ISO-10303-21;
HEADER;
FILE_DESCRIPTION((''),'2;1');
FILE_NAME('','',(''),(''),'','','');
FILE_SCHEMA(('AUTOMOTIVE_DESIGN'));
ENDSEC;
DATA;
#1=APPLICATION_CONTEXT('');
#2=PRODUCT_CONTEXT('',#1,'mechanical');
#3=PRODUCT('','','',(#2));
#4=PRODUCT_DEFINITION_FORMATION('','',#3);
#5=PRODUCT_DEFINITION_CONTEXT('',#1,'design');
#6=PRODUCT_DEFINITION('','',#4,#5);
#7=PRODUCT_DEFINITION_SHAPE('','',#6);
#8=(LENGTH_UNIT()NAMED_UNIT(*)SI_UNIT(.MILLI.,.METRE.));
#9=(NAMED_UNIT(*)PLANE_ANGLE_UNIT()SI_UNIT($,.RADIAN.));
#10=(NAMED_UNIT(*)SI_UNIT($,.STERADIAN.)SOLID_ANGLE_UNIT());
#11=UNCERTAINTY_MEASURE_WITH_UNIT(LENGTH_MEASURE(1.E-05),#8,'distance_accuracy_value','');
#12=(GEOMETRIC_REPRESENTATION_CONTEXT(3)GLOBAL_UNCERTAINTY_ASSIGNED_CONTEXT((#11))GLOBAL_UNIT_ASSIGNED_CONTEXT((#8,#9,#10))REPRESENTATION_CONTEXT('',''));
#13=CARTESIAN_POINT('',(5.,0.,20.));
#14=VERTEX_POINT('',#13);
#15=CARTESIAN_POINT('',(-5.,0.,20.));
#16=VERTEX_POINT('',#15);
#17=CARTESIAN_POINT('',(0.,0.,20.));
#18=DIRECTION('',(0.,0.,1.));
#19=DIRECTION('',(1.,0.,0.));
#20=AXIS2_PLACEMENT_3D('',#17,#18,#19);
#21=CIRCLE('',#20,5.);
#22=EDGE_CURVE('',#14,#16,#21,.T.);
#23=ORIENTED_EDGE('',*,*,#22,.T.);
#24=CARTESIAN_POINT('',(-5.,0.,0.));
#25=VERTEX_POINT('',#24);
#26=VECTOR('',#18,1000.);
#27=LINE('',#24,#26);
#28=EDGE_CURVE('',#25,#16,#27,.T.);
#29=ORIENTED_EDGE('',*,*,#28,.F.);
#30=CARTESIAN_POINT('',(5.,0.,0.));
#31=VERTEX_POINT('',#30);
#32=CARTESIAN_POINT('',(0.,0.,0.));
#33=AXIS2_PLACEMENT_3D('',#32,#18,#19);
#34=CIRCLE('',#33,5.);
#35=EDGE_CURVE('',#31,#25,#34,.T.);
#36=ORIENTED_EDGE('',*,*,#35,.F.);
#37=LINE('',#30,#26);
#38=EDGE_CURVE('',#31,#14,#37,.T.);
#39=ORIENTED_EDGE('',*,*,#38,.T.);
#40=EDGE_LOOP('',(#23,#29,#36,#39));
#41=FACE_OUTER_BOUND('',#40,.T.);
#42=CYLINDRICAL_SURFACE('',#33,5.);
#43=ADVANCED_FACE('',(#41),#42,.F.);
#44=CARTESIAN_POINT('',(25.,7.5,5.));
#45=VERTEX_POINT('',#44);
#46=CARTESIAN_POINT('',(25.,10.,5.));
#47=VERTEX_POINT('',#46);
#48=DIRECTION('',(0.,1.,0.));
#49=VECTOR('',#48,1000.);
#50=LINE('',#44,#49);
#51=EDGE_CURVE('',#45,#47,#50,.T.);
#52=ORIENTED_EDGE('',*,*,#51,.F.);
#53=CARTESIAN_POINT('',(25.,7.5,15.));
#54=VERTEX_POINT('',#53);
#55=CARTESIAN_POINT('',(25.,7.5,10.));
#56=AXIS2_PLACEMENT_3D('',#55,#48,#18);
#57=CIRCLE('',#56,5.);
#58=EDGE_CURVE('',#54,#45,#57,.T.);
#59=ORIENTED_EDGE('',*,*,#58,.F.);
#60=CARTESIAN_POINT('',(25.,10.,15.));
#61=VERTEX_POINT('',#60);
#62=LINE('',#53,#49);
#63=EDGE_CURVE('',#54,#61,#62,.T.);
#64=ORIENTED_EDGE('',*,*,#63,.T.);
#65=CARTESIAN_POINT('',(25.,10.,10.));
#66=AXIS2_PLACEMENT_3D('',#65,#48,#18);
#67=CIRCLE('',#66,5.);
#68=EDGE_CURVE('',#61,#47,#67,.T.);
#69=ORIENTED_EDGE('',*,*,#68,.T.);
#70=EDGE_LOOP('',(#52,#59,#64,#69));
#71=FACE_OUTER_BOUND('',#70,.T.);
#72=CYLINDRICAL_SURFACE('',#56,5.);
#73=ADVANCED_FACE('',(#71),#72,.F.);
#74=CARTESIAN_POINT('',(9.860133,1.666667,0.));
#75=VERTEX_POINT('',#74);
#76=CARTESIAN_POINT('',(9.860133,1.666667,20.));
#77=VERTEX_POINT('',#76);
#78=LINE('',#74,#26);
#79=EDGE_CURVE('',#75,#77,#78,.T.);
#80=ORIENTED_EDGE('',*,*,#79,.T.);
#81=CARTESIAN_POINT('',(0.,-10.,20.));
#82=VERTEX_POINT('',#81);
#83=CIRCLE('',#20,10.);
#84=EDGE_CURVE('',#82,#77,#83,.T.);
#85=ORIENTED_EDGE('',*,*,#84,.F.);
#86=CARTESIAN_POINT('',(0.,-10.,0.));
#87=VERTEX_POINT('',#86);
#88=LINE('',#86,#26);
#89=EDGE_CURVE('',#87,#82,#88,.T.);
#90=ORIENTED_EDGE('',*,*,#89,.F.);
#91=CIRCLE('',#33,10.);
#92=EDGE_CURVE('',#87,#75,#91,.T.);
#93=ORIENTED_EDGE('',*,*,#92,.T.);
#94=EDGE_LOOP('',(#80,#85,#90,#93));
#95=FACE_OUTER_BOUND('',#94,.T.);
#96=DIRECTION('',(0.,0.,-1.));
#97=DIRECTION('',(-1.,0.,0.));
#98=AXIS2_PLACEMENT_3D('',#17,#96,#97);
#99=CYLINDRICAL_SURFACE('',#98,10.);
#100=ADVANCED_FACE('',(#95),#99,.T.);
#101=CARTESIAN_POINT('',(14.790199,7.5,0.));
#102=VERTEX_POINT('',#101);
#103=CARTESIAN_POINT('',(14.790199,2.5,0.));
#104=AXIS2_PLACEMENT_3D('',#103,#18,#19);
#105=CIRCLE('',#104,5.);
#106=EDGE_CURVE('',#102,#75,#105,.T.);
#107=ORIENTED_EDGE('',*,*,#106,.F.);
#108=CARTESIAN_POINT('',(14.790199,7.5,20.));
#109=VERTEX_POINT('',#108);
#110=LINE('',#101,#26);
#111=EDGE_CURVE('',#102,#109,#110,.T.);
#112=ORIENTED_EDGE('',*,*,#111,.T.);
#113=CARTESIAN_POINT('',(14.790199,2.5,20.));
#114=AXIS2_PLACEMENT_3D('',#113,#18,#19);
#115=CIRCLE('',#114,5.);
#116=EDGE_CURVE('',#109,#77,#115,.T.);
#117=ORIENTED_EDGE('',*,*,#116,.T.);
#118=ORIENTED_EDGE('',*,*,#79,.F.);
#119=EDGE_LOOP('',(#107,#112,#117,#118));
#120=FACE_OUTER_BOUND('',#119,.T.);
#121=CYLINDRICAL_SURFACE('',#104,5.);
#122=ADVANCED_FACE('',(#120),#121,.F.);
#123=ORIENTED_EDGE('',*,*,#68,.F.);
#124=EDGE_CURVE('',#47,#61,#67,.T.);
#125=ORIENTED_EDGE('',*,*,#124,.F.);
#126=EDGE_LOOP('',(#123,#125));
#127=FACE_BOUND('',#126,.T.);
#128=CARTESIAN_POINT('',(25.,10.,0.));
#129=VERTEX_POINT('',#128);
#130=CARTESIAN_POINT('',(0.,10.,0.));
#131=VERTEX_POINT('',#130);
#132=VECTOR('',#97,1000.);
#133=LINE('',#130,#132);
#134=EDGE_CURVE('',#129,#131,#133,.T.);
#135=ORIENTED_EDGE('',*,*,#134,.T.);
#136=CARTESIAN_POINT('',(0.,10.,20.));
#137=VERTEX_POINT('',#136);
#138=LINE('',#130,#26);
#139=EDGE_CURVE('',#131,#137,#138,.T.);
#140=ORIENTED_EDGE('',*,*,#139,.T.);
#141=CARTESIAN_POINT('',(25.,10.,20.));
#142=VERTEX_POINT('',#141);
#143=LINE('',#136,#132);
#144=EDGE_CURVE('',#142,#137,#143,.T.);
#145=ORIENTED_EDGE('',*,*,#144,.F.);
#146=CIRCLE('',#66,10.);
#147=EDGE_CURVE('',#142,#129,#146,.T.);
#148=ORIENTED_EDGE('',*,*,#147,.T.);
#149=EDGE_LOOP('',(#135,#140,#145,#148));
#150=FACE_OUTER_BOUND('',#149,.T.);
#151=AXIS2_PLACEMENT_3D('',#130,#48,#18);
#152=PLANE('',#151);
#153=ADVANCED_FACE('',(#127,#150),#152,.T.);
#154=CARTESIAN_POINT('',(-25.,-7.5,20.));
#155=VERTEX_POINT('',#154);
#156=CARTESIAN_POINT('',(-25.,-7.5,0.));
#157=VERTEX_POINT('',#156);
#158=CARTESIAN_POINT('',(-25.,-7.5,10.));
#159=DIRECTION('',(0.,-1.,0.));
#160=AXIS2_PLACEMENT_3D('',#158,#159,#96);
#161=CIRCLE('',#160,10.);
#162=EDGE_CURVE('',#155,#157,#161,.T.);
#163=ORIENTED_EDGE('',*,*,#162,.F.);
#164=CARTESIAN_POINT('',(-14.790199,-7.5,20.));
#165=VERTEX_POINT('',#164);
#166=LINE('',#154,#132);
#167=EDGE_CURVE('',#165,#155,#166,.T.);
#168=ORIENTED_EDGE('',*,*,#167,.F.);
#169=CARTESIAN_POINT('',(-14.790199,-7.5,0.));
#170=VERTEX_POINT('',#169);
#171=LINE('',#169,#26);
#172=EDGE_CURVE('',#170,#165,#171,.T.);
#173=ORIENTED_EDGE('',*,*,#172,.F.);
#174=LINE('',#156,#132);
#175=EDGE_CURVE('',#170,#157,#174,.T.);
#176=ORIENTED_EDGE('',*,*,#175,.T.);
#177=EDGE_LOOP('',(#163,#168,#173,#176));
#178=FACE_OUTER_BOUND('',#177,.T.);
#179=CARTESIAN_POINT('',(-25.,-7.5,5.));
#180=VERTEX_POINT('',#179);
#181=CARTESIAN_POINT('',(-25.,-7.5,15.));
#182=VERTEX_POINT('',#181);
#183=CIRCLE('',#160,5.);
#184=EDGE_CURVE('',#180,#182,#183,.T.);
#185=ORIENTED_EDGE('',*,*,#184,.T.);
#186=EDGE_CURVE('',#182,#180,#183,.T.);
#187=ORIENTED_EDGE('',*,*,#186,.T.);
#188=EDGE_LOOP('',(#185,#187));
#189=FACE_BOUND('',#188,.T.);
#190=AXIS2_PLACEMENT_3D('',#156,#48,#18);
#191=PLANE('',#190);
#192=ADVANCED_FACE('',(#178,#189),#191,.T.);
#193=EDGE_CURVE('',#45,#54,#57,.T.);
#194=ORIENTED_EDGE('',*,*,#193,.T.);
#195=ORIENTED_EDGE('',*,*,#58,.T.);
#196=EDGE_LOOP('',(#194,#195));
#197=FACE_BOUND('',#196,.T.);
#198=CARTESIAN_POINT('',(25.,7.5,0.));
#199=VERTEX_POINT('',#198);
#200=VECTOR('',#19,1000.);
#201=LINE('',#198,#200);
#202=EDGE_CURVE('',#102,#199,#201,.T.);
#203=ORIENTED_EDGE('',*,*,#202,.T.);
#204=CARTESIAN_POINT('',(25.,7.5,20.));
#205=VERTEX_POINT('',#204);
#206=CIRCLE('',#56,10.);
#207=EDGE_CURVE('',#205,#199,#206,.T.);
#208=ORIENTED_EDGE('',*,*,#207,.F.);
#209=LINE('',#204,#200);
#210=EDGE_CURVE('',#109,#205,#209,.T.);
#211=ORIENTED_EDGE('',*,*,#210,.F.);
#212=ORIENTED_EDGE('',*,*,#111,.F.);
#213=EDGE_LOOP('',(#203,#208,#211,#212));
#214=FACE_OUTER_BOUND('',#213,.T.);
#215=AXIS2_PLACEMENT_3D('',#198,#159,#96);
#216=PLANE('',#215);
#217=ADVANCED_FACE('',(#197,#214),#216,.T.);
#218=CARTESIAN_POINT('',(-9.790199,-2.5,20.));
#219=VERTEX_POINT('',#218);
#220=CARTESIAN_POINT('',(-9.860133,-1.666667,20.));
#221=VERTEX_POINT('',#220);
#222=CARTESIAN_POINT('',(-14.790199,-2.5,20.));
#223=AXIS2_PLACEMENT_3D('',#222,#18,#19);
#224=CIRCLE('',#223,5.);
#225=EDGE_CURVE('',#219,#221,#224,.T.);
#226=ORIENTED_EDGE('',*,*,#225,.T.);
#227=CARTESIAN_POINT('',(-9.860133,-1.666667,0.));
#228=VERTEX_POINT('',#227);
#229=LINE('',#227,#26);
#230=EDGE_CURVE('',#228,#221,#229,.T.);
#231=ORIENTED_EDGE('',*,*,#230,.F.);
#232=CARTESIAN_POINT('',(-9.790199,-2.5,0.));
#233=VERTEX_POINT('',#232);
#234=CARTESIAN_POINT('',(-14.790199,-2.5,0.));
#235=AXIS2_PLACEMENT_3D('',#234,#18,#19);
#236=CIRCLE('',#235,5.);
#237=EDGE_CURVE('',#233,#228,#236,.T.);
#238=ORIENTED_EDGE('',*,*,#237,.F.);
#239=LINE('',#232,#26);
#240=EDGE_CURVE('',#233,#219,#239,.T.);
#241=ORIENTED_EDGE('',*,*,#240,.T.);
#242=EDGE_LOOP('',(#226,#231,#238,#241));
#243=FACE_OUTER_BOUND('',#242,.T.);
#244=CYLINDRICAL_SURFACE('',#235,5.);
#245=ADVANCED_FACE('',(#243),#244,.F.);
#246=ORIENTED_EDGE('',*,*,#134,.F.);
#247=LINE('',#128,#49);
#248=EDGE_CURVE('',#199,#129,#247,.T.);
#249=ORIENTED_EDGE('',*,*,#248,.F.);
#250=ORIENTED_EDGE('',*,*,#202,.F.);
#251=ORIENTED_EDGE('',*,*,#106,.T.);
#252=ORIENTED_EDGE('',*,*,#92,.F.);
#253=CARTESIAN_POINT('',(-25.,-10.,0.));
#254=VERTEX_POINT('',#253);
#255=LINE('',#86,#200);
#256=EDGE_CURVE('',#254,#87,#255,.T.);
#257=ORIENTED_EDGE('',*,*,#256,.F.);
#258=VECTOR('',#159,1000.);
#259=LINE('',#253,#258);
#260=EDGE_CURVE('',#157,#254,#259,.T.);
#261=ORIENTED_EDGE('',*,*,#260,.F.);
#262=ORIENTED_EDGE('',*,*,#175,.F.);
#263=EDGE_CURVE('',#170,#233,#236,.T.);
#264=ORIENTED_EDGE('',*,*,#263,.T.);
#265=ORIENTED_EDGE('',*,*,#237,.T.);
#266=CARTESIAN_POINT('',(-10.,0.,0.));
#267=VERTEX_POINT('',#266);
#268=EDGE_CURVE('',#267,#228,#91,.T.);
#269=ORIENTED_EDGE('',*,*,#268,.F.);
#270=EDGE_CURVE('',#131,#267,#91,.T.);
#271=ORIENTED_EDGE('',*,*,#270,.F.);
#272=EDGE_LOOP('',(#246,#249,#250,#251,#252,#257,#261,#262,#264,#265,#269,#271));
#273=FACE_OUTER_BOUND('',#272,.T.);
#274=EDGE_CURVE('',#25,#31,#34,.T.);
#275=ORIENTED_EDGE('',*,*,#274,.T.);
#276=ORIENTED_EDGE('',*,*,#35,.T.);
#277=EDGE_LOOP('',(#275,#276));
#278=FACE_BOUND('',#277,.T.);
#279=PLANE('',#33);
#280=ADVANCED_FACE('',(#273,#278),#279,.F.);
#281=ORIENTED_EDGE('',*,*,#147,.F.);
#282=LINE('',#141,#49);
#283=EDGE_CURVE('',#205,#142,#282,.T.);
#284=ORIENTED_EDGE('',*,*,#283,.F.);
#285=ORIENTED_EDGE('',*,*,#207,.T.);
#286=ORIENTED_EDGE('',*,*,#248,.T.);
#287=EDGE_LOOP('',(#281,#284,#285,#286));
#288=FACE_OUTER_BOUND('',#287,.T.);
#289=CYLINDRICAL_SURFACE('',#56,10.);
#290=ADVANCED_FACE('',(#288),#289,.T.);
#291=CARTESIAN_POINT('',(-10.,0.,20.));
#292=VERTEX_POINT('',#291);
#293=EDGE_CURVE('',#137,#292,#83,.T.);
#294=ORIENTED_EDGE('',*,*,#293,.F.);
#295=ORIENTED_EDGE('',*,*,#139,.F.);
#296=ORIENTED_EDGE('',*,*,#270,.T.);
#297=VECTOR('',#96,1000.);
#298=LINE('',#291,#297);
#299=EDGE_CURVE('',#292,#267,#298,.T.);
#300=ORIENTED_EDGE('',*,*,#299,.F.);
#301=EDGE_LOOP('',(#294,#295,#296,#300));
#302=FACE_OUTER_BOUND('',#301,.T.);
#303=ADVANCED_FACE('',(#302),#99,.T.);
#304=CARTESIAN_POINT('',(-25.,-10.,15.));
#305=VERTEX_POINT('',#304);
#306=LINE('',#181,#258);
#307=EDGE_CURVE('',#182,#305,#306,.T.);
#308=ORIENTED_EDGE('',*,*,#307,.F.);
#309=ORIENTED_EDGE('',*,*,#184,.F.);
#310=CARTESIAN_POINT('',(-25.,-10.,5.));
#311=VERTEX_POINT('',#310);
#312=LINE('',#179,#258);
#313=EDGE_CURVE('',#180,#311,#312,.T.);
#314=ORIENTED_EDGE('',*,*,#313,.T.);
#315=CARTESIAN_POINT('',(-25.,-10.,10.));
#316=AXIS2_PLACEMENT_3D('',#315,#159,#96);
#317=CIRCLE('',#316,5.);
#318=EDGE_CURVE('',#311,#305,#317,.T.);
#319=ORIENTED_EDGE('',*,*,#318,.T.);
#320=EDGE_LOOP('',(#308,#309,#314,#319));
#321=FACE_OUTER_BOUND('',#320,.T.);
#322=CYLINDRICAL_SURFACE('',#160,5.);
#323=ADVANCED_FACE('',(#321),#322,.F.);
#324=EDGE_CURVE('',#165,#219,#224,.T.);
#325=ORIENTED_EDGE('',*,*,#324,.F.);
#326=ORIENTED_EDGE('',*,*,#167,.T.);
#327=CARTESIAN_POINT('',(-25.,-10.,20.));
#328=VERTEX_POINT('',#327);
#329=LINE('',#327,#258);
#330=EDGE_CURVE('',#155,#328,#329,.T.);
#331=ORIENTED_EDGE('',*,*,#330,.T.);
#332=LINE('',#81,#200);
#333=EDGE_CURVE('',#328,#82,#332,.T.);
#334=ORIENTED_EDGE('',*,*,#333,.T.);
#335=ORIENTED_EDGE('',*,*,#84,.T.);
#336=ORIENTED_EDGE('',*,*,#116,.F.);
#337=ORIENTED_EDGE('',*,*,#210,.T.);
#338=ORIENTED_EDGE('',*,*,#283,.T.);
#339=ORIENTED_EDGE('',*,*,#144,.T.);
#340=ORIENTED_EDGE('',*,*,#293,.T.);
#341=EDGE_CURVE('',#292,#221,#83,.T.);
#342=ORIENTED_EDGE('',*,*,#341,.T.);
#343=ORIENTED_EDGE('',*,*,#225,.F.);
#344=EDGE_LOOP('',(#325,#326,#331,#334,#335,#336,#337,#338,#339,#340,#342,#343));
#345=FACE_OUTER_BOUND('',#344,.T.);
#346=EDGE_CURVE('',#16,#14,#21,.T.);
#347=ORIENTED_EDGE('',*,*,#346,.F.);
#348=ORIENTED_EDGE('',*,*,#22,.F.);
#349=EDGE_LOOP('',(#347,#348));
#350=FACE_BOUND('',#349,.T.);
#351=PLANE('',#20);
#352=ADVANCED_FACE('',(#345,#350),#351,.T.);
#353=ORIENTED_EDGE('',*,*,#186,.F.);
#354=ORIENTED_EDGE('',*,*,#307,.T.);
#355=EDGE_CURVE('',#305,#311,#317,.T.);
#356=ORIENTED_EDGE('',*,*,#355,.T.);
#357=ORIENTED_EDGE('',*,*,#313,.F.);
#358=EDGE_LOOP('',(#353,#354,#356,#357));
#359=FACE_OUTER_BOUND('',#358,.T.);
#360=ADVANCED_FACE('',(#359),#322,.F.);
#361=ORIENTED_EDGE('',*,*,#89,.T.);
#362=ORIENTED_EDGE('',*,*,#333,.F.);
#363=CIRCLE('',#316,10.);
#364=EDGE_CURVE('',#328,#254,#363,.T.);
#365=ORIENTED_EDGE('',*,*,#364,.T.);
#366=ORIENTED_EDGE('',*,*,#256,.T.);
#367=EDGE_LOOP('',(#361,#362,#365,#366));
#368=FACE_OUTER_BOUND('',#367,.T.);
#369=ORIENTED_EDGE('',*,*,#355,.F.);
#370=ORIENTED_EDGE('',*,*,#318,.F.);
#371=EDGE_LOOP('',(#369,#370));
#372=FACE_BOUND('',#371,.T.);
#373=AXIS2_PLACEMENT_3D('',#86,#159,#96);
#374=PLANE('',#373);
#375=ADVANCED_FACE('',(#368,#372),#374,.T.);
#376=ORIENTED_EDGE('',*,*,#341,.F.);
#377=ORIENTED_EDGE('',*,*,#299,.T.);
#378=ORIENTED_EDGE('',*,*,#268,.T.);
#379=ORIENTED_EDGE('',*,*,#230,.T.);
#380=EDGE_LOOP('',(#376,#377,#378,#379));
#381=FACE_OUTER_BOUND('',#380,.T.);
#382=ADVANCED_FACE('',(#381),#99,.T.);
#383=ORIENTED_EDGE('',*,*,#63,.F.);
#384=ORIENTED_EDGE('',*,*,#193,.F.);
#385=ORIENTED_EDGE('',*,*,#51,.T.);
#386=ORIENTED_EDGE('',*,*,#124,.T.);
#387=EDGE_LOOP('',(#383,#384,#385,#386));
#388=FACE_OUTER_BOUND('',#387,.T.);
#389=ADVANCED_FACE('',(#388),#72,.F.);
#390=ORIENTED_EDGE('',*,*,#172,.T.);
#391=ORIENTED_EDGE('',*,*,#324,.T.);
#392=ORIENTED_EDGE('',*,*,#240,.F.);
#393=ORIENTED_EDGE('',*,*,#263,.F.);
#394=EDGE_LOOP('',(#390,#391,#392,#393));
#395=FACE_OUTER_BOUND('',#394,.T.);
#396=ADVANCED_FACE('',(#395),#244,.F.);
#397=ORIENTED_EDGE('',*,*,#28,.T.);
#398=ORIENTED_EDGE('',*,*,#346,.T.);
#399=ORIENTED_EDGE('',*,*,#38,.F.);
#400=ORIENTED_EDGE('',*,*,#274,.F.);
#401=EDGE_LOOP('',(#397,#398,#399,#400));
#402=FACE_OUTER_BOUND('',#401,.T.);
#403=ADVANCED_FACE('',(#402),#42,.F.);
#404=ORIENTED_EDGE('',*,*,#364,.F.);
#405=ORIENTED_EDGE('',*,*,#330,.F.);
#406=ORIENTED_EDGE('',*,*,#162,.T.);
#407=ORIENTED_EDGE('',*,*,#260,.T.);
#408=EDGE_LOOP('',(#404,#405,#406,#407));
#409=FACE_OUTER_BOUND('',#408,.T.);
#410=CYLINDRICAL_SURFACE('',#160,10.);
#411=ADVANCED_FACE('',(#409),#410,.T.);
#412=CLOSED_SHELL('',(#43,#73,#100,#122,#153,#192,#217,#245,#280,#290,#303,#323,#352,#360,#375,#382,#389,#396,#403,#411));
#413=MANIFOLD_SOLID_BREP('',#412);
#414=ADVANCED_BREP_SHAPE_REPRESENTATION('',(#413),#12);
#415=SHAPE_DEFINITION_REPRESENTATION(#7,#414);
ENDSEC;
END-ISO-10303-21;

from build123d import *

# Parameters (mm, degrees)
HUB_SKETCH_20_R            = 10
HUB_CYLINDER_20_DEPTH      = 20
FIRST_START                = -20
FIRST_ARM_DEPTH            = 20
SECOND_START               = -20
SECOND_ARM_DEPTH           = 20
TAB_A_DEPTH                = 2.5
TAB_B_DEPTH                = 2.5
TAB_B_HOLE_SKETCH_10_R     = 5
TAB_B_HOLE_10_DEPTH        = 2.5
TAB_A_HOLE_SKETCH_10_R     = 5
TAB_A_HOLE_10_DEPTH        = 2.5
HUB_CROSS_BORE_SKETCH_10_R = 5
HUB_CROSS_BORE_10_DEPTH    = 20


with BuildPart() as part:
    # Hub Sketch Ø20 → Hub Cylinder Ø20 (new body)
    with BuildSketch(Plane.XY):
        Circle(HUB_SKETCH_20_R)
    extrude(amount=HUB_CYLINDER_20_DEPTH)

    # First Arm Sketch → First Arm (add)
    with BuildSketch(Plane.XY.offset(20).offset(FIRST_START)):
        with BuildLine():
            Line((0, 10), (25, 10))
            Line((25, 10), (25, 7.5))
            Line((25, 7.5), (6.614378278, 7.5))
            ThreePointArc((6.614378278, 7.5), (3.535533906, 9.354143467), (0, 10))
        make_face()
        with BuildLine():
            Line((0, -10), (-25, -10))
            Line((-25, -10), (-25, -7.5))
            Line((-25, -7.5), (-6.614378278, -7.5))
            ThreePointArc((-6.614378278, -7.5), (-3.535533906, -9.354143467), (0, -10))
        make_face()
    extrude(amount=FIRST_ARM_DEPTH)

    # Second Arm Sketch → Second Arm (add)
    with BuildSketch(Plane.XY.offset(20).offset(SECOND_START)):
        with BuildLine():
            ThreePointArc((-9.860132972, -1.666666667), (-10.971386379, -5.727486122), (-14.790199458, -7.5))
            Line((-14.790199458, -7.5), (-6.614378278, -7.5))
            ThreePointArc((-6.614378278, -7.5), (-8.738382269, -4.86216776), (-9.860132972, -1.666666667))
        make_face()
        with BuildLine():
            ThreePointArc((9.860132972, 1.666666667), (10.971386379, 5.727486122), (14.790199458, 7.5))
            Line((14.790199458, 7.5), (6.614378278, 7.5))
            ThreePointArc((6.614378278, 7.5), (8.738382269, 4.86216776), (9.860132972, 1.666666667))
        make_face()
    extrude(amount=SECOND_ARM_DEPTH)

    # Tab A Sketch → Tab A (add)
    with BuildSketch(Plane.XZ.offset(10)):
        with BuildLine():
            Line((-25, 20), (-25, 0))
            ThreePointArc((-25, 0), (-35, 10), (-25, 20))
        make_face()
    extrude(amount=-TAB_A_DEPTH)

    # Tab B Sketch → Tab B (add)
    with BuildSketch(Plane(origin=(0, 10, 0), x_dir=(1, 0, 0), z_dir=(0, 1, 0))):
        with BuildLine():
            Line((25, 0), (25, -20))
            ThreePointArc((25, -20), (35, -10), (25, 0))
        make_face()
    extrude(amount=-TAB_B_DEPTH)

    # Tab B Hole Sketch Ø10 → Tab B Hole Ø10 (cut)
    with BuildSketch(Plane(origin=(0, 10, 0), x_dir=(1, 0, 0), z_dir=(0, 1, 0))):
        with Locations(Location((25, -10, 0), (0, 0, 270))):
            Circle(TAB_B_HOLE_SKETCH_10_R)
    extrude(amount=-TAB_B_HOLE_10_DEPTH, mode=Mode.SUBTRACT)

    # Tab A Hole Sketch Ø10 → Tab A Hole Ø10 (cut)
    with BuildSketch(Plane.XZ.offset(10)):
        with Locations(Location((-25, 10, 0), (0, 0, 270))):
            Circle(TAB_A_HOLE_SKETCH_10_R)
    extrude(amount=-TAB_A_HOLE_10_DEPTH, mode=Mode.SUBTRACT)

    # Hub Cross Bore Sketch Ø10 → Hub Cross Bore Ø10 (cut)
    with BuildSketch(Plane.XY.offset(20)):
        Circle(HUB_CROSS_BORE_SKETCH_10_R)
    extrude(amount=-HUB_CROSS_BORE_10_DEPTH, mode=Mode.SUBTRACT)


solid = part.part
